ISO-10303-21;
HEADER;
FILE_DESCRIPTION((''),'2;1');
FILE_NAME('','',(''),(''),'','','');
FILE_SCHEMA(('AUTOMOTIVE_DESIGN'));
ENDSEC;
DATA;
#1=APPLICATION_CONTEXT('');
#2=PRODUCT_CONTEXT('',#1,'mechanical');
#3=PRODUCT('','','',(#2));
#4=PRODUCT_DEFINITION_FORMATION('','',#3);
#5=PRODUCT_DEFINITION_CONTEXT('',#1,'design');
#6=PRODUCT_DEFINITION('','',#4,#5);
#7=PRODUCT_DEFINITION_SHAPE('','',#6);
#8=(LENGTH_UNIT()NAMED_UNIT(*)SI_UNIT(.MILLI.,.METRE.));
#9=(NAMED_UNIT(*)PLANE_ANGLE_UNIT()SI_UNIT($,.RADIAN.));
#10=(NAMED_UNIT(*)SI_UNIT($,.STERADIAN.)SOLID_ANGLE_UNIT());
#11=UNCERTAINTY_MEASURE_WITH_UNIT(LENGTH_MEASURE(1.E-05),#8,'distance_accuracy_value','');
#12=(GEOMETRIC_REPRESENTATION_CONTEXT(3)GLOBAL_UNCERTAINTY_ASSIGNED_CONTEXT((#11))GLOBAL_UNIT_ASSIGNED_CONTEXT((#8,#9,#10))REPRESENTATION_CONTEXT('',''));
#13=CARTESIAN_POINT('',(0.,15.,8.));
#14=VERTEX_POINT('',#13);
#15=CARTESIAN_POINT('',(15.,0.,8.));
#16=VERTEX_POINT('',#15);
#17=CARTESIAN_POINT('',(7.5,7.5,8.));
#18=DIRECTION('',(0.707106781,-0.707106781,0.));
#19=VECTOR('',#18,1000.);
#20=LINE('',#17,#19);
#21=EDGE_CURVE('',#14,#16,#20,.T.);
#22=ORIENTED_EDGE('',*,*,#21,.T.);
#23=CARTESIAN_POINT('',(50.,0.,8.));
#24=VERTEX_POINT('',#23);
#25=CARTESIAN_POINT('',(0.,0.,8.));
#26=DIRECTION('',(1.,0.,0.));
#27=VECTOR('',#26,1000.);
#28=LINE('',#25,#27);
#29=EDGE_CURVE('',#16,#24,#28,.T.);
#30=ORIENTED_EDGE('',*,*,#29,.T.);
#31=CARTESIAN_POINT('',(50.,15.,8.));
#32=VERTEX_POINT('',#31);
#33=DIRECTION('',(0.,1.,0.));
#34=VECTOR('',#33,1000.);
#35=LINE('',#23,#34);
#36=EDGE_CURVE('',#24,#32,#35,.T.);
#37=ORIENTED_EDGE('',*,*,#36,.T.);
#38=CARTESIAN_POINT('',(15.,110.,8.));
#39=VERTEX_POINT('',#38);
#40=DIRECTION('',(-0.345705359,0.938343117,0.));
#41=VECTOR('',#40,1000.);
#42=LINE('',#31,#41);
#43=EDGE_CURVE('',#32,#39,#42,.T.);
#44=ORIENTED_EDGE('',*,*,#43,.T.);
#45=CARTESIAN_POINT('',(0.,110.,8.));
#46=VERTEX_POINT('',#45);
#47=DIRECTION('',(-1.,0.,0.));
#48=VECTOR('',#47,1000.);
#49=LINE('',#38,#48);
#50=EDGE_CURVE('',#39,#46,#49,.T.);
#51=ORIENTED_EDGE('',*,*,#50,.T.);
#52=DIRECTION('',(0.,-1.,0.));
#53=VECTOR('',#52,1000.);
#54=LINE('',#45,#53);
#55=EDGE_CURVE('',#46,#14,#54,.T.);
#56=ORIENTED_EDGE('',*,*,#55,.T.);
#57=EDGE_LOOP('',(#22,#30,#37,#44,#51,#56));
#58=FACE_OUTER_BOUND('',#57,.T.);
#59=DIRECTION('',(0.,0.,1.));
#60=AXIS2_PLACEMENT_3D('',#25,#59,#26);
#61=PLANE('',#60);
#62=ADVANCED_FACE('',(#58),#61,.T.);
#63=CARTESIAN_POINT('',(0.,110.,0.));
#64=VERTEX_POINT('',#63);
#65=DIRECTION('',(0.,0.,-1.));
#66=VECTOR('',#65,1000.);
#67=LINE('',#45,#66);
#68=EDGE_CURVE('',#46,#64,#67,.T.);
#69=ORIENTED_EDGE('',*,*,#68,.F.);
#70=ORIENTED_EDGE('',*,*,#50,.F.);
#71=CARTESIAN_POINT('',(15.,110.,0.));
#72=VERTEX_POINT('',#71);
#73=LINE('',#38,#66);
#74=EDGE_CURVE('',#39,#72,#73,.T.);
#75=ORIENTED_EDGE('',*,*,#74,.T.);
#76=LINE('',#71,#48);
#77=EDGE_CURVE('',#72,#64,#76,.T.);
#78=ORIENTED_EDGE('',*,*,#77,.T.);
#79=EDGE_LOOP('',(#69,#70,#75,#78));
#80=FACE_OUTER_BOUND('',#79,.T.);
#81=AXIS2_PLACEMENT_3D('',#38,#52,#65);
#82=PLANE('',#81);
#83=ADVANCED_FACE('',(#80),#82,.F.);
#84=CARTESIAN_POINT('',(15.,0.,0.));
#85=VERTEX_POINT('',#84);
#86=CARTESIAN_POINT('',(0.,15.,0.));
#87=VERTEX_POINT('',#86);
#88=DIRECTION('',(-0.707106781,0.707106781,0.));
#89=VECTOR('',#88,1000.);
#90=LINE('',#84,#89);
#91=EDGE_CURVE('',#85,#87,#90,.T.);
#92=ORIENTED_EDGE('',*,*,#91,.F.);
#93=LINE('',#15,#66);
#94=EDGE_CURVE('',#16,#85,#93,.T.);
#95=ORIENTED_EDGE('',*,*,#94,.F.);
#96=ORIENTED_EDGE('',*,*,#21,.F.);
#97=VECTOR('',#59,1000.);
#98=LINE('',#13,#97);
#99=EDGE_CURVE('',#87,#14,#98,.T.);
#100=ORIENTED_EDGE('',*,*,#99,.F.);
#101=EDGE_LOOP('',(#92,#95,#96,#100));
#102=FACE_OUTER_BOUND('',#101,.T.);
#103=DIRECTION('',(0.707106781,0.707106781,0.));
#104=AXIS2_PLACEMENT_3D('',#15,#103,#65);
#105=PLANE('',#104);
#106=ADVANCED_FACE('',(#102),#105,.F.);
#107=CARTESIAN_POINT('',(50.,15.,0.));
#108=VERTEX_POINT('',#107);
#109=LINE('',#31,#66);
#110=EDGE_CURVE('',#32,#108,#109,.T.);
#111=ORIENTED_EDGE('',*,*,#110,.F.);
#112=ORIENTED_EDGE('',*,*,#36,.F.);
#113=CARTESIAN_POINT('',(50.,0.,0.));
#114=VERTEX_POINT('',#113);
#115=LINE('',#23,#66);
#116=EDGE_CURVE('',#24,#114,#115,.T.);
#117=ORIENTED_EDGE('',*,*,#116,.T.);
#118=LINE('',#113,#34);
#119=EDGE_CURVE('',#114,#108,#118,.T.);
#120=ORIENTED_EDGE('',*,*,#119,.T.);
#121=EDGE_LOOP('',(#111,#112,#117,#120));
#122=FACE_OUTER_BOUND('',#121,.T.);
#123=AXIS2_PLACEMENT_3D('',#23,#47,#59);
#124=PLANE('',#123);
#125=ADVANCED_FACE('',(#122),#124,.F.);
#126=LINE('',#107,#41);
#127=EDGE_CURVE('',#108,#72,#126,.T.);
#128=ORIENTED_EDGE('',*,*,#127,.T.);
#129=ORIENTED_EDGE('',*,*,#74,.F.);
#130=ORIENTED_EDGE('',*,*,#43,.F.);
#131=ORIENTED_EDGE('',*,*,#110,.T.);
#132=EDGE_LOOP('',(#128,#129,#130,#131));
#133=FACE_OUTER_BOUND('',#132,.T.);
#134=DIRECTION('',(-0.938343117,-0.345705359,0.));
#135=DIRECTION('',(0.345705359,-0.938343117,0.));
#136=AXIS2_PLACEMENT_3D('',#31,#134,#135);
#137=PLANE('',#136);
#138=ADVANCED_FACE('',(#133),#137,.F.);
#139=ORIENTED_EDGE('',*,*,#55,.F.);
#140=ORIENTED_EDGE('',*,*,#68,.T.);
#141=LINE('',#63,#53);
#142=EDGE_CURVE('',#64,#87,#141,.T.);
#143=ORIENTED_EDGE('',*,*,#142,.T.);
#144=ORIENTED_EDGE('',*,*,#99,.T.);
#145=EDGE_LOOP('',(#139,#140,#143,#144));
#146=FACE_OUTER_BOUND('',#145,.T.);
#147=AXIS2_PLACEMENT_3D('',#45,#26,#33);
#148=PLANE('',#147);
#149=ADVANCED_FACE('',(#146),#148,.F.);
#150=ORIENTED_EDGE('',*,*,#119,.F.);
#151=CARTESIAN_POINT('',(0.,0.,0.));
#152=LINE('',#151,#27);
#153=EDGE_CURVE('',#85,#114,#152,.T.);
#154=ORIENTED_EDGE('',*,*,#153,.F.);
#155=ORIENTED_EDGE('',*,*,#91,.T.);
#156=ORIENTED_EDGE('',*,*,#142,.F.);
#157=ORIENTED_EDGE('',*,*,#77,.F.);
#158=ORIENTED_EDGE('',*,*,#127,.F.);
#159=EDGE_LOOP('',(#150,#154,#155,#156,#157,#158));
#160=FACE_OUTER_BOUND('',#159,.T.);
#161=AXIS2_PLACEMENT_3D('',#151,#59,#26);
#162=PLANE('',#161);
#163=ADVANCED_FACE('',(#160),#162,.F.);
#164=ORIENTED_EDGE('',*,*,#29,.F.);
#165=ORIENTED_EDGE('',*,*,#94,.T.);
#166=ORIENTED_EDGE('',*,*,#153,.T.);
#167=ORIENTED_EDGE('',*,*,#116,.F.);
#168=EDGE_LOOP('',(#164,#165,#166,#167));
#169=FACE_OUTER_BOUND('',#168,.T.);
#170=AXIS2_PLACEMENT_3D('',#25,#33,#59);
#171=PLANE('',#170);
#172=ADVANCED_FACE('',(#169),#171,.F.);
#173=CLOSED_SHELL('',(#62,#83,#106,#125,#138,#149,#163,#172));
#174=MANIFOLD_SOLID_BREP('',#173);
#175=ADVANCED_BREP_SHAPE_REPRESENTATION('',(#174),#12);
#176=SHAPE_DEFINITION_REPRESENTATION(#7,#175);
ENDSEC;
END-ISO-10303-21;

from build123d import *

# Parameters (mm, degrees)
BOSS_EXTRUDE1_DEPTH = 8
CHAMFER1_SIZE       = 15


with BuildPart() as part:
    # Sketch1 → Boss-Extrude1 (new body)
    with BuildSketch(Plane.XY):
        Polygon((0, 0), (50, 0), (50, 15), (15, 110), (0, 110), align=None)
    extrude(amount=BOSS_EXTRUDE1_DEPTH)

    # Chamfer1
    chamfer1_edges = [part.edges().sort_by_distance(p)[0] for p in [
        (0, 0, 4),
    ]]
    chamfer(chamfer1_edges, length=CHAMFER1_SIZE)


solid = part.part
